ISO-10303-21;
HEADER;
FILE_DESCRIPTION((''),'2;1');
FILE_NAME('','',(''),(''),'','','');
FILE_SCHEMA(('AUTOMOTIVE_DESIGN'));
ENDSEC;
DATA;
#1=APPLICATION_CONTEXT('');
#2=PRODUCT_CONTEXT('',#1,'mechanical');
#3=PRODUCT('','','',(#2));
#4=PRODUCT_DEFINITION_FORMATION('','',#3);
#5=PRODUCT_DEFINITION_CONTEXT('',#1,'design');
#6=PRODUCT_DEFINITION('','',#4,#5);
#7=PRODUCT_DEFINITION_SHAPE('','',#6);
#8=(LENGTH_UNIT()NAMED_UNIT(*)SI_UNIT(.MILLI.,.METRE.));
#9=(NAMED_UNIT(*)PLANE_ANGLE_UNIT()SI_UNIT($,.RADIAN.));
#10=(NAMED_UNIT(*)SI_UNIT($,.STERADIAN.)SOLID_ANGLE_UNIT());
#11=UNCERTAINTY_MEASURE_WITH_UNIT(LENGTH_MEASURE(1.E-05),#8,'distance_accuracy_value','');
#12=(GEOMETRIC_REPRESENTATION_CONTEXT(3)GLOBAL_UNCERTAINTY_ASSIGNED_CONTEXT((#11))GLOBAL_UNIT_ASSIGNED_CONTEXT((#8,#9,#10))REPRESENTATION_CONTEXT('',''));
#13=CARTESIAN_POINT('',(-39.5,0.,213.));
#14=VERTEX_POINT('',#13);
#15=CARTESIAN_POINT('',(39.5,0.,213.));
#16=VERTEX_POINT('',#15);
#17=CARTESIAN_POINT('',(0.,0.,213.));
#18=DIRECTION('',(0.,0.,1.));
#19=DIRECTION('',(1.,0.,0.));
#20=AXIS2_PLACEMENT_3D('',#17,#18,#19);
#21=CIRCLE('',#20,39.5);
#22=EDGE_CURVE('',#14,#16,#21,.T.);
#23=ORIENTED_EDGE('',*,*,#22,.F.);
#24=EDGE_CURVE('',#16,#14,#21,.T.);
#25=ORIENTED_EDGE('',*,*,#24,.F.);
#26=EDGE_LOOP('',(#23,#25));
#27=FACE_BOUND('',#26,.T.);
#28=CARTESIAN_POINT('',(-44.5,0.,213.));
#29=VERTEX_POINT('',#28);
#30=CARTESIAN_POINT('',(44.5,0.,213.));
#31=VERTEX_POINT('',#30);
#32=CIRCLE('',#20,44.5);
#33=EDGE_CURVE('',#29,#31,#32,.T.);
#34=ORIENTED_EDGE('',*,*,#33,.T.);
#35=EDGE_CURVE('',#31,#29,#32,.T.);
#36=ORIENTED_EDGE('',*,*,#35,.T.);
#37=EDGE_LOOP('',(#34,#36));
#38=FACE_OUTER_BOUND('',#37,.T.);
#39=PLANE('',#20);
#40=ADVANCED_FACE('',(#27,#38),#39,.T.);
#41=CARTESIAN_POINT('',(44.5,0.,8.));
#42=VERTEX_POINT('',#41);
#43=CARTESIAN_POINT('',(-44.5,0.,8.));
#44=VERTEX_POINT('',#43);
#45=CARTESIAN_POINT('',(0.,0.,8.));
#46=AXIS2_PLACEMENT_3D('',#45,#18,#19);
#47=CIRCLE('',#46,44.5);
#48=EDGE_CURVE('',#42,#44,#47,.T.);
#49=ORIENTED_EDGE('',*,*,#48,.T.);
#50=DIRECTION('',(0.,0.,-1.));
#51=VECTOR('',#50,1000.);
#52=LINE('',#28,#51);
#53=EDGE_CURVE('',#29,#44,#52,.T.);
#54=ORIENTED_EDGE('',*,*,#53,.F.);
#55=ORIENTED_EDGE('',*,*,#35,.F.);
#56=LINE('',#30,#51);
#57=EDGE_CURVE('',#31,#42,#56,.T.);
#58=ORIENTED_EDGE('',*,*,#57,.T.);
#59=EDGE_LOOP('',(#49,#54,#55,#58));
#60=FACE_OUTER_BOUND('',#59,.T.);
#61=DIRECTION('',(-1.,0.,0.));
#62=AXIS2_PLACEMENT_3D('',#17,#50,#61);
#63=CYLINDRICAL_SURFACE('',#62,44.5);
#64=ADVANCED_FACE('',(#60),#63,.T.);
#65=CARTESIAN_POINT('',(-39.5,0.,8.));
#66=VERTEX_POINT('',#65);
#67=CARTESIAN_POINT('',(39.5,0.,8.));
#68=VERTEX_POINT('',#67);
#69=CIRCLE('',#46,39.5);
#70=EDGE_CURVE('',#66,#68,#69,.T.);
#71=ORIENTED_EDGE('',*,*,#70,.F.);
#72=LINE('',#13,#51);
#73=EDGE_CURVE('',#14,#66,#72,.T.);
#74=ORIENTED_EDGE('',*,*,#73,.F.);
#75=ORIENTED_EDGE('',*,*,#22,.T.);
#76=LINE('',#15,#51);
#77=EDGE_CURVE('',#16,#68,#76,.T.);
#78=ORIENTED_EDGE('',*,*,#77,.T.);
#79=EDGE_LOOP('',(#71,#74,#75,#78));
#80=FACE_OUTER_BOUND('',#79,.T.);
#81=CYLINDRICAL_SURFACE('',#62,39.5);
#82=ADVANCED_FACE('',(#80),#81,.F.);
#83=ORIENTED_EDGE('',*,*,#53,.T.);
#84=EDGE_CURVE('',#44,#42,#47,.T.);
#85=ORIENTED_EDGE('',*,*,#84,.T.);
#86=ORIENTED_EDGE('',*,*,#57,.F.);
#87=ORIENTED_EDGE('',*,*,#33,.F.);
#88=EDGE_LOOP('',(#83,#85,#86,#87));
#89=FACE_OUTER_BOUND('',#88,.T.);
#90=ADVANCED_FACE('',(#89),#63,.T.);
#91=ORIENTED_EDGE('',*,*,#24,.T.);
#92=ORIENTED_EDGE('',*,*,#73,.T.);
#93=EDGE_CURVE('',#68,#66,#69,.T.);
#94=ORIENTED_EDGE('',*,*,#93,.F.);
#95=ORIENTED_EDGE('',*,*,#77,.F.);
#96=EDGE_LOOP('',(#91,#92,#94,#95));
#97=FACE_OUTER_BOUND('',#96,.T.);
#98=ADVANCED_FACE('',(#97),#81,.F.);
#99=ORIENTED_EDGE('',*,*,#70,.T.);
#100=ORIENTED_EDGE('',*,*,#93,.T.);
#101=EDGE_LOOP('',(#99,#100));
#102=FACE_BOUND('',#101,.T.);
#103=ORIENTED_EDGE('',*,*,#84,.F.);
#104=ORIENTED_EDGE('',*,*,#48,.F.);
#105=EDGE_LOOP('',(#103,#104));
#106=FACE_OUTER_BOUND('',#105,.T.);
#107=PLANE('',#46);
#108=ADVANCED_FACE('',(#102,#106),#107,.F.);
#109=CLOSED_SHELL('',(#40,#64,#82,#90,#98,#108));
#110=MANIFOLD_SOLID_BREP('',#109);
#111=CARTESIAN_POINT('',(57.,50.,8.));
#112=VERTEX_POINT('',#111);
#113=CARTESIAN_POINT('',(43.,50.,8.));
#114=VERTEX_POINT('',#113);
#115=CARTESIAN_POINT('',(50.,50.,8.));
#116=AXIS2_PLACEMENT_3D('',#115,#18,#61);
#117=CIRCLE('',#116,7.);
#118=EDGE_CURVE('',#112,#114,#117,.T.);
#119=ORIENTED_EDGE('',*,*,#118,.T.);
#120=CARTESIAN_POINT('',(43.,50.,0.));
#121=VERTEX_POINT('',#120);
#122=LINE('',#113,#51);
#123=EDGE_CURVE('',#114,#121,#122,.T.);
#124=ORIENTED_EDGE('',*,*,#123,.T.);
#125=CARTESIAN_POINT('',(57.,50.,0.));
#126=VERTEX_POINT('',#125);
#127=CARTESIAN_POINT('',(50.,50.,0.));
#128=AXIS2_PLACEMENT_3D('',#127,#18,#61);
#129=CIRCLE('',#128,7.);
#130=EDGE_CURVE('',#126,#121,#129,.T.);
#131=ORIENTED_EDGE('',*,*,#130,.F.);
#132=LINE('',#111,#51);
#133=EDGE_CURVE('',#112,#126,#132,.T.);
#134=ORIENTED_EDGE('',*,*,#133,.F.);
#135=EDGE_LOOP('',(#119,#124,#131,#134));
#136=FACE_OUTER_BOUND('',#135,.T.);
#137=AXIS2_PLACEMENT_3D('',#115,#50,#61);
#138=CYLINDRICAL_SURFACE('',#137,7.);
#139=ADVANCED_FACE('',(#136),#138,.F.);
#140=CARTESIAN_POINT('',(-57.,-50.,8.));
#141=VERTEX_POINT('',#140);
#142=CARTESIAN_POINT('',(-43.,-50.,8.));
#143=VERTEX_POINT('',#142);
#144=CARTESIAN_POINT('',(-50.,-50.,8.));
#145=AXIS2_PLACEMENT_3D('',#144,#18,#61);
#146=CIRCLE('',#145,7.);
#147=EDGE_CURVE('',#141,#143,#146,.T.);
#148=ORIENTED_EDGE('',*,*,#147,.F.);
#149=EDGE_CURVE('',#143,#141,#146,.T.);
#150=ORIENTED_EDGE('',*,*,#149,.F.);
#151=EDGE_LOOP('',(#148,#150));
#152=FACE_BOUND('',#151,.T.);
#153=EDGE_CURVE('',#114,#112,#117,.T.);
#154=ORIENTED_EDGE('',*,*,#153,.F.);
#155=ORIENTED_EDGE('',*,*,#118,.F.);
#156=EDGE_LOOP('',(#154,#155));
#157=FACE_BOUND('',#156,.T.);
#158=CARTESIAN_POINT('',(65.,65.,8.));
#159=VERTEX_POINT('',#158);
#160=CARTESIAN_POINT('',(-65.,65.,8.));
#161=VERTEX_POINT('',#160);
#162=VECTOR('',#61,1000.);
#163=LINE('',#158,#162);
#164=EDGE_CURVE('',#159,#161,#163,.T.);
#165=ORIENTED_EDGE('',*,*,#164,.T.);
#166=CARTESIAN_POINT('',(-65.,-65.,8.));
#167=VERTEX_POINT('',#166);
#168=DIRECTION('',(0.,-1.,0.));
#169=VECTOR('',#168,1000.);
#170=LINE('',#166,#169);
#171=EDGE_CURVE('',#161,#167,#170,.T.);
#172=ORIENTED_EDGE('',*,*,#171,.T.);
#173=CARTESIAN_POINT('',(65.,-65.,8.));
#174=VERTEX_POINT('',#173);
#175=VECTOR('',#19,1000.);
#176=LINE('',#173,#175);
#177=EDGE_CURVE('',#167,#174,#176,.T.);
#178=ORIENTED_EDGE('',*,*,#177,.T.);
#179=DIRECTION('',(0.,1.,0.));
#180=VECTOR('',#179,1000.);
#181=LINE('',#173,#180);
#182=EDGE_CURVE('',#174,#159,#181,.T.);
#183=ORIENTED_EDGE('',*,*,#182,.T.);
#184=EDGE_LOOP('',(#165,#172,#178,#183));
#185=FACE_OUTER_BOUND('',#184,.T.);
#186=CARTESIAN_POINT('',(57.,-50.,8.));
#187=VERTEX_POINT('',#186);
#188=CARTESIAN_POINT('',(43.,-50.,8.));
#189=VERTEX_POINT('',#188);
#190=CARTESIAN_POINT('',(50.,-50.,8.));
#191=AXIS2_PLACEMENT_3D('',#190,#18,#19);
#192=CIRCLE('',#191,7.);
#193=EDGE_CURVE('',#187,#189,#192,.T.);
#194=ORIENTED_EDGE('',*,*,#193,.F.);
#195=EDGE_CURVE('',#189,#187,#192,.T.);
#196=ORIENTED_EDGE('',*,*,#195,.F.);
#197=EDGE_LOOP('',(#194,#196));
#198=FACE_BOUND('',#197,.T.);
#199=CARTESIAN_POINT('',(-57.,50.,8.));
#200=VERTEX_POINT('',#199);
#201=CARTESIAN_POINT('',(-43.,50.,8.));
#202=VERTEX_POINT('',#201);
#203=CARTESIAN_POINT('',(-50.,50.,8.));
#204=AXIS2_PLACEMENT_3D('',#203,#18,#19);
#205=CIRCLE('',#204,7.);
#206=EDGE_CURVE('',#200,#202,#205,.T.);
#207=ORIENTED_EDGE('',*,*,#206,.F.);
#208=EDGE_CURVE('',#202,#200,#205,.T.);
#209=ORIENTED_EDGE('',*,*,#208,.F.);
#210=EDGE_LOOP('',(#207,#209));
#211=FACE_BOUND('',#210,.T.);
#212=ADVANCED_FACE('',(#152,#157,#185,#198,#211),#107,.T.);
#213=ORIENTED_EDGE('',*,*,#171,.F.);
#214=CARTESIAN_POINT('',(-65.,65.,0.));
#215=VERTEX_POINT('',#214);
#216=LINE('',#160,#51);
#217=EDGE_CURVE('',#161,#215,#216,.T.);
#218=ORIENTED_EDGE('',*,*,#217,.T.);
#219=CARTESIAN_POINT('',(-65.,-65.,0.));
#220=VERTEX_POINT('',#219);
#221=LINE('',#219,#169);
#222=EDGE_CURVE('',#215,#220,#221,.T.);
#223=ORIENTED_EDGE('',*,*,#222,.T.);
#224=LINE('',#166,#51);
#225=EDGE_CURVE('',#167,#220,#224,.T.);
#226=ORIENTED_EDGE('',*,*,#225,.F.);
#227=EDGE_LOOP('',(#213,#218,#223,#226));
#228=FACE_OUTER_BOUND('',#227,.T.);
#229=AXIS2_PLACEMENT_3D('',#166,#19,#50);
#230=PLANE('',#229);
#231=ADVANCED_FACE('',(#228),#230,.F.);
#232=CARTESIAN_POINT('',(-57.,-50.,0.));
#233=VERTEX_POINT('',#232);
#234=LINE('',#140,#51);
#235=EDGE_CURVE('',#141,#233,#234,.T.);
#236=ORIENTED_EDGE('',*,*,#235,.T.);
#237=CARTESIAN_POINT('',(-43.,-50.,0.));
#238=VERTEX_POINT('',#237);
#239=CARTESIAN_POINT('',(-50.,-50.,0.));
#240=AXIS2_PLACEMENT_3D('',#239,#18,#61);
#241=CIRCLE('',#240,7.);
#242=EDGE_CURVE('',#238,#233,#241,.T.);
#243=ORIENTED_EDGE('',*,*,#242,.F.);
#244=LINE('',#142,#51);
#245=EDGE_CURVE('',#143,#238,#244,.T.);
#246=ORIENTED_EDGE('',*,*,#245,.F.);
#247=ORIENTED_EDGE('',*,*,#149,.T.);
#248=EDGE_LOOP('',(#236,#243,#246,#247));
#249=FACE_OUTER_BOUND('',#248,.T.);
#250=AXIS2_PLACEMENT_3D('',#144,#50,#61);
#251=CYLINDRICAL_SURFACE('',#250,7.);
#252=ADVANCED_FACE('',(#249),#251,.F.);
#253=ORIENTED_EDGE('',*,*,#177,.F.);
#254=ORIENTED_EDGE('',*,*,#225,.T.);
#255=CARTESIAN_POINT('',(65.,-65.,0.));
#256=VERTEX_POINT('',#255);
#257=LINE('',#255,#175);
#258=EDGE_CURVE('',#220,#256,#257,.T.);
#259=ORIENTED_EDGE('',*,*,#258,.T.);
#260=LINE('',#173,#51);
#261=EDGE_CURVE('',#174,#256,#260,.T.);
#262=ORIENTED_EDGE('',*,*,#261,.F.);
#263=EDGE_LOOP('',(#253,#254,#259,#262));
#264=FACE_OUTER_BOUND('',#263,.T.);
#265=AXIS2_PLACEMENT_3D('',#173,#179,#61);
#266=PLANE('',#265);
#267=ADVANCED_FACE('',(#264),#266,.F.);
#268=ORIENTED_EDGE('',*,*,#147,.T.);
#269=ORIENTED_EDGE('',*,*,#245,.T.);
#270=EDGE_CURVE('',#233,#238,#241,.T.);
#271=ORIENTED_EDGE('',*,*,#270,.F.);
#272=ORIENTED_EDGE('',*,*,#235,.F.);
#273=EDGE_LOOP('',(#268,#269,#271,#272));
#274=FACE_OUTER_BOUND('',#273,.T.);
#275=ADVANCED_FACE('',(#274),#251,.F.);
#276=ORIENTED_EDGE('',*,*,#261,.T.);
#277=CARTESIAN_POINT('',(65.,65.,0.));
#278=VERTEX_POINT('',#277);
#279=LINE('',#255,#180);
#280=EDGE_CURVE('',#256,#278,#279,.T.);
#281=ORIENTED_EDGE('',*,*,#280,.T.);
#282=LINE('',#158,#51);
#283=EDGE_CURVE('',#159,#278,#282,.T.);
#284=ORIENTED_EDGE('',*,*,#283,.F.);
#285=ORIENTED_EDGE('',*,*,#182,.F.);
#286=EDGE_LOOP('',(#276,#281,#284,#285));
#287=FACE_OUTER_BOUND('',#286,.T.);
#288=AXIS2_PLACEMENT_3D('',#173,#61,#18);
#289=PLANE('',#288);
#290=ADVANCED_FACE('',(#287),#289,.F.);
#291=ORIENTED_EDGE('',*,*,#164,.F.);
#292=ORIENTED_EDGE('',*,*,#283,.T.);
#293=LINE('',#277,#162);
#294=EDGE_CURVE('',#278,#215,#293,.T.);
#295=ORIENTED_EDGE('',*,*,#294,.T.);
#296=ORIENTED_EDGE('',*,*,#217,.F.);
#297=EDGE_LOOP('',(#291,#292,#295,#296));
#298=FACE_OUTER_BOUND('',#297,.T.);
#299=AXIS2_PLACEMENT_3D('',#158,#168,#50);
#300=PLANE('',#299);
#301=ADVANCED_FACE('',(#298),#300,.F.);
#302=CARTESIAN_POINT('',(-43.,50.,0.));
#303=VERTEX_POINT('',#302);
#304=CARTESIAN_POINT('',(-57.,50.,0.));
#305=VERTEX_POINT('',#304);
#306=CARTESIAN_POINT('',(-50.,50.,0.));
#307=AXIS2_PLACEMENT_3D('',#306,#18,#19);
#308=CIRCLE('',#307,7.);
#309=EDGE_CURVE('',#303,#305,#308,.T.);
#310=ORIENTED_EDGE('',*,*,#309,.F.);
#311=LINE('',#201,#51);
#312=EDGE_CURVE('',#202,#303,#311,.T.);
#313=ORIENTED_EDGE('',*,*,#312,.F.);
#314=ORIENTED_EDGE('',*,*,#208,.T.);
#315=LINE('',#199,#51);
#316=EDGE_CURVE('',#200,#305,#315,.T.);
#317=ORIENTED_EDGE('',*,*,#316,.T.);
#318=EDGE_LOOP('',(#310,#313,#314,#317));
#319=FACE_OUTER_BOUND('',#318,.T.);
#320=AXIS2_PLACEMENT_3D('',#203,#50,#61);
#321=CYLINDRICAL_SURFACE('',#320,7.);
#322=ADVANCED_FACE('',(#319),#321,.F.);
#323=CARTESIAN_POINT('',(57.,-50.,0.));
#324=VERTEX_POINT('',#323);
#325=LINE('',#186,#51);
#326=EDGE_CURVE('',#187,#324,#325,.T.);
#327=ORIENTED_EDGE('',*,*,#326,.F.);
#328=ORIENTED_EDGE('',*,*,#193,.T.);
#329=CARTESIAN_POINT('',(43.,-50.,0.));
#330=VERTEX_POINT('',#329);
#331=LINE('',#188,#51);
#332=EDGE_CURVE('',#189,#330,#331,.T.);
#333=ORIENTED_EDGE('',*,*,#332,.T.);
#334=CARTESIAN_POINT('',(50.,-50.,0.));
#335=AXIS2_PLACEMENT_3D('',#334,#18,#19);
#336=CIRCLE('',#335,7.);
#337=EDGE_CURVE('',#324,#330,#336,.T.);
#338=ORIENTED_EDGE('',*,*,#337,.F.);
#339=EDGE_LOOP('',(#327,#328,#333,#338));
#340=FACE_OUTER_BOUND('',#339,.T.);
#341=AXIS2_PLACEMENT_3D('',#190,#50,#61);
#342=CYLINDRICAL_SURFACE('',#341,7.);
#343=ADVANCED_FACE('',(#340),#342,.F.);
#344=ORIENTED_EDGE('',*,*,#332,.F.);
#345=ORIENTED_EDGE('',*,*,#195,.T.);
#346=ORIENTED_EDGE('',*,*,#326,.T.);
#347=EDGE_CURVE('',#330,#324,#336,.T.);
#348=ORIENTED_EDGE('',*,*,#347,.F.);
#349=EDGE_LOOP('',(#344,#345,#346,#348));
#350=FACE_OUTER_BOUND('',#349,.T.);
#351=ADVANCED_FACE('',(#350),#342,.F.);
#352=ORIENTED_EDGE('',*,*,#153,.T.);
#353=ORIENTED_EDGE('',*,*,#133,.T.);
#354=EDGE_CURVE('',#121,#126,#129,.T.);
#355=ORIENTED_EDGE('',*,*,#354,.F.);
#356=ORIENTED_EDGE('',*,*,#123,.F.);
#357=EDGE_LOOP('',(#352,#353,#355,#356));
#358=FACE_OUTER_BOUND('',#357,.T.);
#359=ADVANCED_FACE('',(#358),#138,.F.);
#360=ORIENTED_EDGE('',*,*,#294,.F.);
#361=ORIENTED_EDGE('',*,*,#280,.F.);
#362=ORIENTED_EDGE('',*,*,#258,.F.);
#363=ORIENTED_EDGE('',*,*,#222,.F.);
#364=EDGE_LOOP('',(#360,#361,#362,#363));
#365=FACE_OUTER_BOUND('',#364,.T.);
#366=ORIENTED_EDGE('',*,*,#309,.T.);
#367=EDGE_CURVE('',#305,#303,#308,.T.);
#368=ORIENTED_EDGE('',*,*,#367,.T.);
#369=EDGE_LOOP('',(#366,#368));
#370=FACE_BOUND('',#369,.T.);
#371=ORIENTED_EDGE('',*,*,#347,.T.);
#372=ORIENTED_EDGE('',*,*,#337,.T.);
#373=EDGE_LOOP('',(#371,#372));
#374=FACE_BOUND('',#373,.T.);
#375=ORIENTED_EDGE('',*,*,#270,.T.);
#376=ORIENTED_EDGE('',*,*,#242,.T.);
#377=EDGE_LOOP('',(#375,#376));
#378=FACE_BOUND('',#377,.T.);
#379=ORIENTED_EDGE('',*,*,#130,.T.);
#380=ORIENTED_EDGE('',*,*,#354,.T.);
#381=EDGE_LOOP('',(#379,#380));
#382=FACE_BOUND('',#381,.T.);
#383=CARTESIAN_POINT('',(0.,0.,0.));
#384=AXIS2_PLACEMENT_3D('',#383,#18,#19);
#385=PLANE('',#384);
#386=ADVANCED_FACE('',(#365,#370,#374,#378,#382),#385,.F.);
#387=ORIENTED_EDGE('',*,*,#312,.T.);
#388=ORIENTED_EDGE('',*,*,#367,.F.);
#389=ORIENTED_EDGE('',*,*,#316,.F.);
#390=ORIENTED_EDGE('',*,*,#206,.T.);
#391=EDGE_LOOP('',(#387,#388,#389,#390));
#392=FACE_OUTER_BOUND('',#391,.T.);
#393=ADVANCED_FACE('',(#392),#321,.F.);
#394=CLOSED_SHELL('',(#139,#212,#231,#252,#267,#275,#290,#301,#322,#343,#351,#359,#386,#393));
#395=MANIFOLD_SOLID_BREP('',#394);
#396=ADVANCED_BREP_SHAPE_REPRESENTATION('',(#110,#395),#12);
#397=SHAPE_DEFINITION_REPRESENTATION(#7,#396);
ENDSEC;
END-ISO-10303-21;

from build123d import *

# Parameters (mm, degrees)
SKETCH_2_W          = 130
SKETCH_2_H          = 130
SKETCH_2_R          = 7
EXTRUDE_1_DEPTH     = 8
SKETCH12_R          = 44.5
SKETCH12_R_2        = 39.5
MEMBER_89X5_1_DEPTH = 205


with BuildPart() as part:
    # 草图2 → 凸台-拉伸1 (new body)
    with BuildSketch(Plane.XY):
        Rectangle(SKETCH_2_W, SKETCH_2_H)
        with Locations((-50, 50)):
            Circle(SKETCH_2_R, mode=Mode.SUBTRACT)
        with Locations(Location((50, 50, 0), (0, 0, 180))):
            Circle(SKETCH_2_R, mode=Mode.SUBTRACT)
        with Locations((50, -50)):
            Circle(SKETCH_2_R, mode=Mode.SUBTRACT)
        with Locations(Location((-50, -50, 0), (0, 0, 180))):
            Circle(SKETCH_2_R, mode=Mode.SUBTRACT)
    extrude(amount=EXTRUDE_1_DEPTH)


with BuildPart() as body_2:
    # Sketch12 → Member 89X5_1 (new body)
    with BuildSketch(Plane.XY.offset(8)):
        Circle(SKETCH12_R)
        Circle(SKETCH12_R_2, mode=Mode.SUBTRACT)
    extrude(amount=MEMBER_89X5_1_DEPTH)


solid = Compound([part.part, body_2.part])
